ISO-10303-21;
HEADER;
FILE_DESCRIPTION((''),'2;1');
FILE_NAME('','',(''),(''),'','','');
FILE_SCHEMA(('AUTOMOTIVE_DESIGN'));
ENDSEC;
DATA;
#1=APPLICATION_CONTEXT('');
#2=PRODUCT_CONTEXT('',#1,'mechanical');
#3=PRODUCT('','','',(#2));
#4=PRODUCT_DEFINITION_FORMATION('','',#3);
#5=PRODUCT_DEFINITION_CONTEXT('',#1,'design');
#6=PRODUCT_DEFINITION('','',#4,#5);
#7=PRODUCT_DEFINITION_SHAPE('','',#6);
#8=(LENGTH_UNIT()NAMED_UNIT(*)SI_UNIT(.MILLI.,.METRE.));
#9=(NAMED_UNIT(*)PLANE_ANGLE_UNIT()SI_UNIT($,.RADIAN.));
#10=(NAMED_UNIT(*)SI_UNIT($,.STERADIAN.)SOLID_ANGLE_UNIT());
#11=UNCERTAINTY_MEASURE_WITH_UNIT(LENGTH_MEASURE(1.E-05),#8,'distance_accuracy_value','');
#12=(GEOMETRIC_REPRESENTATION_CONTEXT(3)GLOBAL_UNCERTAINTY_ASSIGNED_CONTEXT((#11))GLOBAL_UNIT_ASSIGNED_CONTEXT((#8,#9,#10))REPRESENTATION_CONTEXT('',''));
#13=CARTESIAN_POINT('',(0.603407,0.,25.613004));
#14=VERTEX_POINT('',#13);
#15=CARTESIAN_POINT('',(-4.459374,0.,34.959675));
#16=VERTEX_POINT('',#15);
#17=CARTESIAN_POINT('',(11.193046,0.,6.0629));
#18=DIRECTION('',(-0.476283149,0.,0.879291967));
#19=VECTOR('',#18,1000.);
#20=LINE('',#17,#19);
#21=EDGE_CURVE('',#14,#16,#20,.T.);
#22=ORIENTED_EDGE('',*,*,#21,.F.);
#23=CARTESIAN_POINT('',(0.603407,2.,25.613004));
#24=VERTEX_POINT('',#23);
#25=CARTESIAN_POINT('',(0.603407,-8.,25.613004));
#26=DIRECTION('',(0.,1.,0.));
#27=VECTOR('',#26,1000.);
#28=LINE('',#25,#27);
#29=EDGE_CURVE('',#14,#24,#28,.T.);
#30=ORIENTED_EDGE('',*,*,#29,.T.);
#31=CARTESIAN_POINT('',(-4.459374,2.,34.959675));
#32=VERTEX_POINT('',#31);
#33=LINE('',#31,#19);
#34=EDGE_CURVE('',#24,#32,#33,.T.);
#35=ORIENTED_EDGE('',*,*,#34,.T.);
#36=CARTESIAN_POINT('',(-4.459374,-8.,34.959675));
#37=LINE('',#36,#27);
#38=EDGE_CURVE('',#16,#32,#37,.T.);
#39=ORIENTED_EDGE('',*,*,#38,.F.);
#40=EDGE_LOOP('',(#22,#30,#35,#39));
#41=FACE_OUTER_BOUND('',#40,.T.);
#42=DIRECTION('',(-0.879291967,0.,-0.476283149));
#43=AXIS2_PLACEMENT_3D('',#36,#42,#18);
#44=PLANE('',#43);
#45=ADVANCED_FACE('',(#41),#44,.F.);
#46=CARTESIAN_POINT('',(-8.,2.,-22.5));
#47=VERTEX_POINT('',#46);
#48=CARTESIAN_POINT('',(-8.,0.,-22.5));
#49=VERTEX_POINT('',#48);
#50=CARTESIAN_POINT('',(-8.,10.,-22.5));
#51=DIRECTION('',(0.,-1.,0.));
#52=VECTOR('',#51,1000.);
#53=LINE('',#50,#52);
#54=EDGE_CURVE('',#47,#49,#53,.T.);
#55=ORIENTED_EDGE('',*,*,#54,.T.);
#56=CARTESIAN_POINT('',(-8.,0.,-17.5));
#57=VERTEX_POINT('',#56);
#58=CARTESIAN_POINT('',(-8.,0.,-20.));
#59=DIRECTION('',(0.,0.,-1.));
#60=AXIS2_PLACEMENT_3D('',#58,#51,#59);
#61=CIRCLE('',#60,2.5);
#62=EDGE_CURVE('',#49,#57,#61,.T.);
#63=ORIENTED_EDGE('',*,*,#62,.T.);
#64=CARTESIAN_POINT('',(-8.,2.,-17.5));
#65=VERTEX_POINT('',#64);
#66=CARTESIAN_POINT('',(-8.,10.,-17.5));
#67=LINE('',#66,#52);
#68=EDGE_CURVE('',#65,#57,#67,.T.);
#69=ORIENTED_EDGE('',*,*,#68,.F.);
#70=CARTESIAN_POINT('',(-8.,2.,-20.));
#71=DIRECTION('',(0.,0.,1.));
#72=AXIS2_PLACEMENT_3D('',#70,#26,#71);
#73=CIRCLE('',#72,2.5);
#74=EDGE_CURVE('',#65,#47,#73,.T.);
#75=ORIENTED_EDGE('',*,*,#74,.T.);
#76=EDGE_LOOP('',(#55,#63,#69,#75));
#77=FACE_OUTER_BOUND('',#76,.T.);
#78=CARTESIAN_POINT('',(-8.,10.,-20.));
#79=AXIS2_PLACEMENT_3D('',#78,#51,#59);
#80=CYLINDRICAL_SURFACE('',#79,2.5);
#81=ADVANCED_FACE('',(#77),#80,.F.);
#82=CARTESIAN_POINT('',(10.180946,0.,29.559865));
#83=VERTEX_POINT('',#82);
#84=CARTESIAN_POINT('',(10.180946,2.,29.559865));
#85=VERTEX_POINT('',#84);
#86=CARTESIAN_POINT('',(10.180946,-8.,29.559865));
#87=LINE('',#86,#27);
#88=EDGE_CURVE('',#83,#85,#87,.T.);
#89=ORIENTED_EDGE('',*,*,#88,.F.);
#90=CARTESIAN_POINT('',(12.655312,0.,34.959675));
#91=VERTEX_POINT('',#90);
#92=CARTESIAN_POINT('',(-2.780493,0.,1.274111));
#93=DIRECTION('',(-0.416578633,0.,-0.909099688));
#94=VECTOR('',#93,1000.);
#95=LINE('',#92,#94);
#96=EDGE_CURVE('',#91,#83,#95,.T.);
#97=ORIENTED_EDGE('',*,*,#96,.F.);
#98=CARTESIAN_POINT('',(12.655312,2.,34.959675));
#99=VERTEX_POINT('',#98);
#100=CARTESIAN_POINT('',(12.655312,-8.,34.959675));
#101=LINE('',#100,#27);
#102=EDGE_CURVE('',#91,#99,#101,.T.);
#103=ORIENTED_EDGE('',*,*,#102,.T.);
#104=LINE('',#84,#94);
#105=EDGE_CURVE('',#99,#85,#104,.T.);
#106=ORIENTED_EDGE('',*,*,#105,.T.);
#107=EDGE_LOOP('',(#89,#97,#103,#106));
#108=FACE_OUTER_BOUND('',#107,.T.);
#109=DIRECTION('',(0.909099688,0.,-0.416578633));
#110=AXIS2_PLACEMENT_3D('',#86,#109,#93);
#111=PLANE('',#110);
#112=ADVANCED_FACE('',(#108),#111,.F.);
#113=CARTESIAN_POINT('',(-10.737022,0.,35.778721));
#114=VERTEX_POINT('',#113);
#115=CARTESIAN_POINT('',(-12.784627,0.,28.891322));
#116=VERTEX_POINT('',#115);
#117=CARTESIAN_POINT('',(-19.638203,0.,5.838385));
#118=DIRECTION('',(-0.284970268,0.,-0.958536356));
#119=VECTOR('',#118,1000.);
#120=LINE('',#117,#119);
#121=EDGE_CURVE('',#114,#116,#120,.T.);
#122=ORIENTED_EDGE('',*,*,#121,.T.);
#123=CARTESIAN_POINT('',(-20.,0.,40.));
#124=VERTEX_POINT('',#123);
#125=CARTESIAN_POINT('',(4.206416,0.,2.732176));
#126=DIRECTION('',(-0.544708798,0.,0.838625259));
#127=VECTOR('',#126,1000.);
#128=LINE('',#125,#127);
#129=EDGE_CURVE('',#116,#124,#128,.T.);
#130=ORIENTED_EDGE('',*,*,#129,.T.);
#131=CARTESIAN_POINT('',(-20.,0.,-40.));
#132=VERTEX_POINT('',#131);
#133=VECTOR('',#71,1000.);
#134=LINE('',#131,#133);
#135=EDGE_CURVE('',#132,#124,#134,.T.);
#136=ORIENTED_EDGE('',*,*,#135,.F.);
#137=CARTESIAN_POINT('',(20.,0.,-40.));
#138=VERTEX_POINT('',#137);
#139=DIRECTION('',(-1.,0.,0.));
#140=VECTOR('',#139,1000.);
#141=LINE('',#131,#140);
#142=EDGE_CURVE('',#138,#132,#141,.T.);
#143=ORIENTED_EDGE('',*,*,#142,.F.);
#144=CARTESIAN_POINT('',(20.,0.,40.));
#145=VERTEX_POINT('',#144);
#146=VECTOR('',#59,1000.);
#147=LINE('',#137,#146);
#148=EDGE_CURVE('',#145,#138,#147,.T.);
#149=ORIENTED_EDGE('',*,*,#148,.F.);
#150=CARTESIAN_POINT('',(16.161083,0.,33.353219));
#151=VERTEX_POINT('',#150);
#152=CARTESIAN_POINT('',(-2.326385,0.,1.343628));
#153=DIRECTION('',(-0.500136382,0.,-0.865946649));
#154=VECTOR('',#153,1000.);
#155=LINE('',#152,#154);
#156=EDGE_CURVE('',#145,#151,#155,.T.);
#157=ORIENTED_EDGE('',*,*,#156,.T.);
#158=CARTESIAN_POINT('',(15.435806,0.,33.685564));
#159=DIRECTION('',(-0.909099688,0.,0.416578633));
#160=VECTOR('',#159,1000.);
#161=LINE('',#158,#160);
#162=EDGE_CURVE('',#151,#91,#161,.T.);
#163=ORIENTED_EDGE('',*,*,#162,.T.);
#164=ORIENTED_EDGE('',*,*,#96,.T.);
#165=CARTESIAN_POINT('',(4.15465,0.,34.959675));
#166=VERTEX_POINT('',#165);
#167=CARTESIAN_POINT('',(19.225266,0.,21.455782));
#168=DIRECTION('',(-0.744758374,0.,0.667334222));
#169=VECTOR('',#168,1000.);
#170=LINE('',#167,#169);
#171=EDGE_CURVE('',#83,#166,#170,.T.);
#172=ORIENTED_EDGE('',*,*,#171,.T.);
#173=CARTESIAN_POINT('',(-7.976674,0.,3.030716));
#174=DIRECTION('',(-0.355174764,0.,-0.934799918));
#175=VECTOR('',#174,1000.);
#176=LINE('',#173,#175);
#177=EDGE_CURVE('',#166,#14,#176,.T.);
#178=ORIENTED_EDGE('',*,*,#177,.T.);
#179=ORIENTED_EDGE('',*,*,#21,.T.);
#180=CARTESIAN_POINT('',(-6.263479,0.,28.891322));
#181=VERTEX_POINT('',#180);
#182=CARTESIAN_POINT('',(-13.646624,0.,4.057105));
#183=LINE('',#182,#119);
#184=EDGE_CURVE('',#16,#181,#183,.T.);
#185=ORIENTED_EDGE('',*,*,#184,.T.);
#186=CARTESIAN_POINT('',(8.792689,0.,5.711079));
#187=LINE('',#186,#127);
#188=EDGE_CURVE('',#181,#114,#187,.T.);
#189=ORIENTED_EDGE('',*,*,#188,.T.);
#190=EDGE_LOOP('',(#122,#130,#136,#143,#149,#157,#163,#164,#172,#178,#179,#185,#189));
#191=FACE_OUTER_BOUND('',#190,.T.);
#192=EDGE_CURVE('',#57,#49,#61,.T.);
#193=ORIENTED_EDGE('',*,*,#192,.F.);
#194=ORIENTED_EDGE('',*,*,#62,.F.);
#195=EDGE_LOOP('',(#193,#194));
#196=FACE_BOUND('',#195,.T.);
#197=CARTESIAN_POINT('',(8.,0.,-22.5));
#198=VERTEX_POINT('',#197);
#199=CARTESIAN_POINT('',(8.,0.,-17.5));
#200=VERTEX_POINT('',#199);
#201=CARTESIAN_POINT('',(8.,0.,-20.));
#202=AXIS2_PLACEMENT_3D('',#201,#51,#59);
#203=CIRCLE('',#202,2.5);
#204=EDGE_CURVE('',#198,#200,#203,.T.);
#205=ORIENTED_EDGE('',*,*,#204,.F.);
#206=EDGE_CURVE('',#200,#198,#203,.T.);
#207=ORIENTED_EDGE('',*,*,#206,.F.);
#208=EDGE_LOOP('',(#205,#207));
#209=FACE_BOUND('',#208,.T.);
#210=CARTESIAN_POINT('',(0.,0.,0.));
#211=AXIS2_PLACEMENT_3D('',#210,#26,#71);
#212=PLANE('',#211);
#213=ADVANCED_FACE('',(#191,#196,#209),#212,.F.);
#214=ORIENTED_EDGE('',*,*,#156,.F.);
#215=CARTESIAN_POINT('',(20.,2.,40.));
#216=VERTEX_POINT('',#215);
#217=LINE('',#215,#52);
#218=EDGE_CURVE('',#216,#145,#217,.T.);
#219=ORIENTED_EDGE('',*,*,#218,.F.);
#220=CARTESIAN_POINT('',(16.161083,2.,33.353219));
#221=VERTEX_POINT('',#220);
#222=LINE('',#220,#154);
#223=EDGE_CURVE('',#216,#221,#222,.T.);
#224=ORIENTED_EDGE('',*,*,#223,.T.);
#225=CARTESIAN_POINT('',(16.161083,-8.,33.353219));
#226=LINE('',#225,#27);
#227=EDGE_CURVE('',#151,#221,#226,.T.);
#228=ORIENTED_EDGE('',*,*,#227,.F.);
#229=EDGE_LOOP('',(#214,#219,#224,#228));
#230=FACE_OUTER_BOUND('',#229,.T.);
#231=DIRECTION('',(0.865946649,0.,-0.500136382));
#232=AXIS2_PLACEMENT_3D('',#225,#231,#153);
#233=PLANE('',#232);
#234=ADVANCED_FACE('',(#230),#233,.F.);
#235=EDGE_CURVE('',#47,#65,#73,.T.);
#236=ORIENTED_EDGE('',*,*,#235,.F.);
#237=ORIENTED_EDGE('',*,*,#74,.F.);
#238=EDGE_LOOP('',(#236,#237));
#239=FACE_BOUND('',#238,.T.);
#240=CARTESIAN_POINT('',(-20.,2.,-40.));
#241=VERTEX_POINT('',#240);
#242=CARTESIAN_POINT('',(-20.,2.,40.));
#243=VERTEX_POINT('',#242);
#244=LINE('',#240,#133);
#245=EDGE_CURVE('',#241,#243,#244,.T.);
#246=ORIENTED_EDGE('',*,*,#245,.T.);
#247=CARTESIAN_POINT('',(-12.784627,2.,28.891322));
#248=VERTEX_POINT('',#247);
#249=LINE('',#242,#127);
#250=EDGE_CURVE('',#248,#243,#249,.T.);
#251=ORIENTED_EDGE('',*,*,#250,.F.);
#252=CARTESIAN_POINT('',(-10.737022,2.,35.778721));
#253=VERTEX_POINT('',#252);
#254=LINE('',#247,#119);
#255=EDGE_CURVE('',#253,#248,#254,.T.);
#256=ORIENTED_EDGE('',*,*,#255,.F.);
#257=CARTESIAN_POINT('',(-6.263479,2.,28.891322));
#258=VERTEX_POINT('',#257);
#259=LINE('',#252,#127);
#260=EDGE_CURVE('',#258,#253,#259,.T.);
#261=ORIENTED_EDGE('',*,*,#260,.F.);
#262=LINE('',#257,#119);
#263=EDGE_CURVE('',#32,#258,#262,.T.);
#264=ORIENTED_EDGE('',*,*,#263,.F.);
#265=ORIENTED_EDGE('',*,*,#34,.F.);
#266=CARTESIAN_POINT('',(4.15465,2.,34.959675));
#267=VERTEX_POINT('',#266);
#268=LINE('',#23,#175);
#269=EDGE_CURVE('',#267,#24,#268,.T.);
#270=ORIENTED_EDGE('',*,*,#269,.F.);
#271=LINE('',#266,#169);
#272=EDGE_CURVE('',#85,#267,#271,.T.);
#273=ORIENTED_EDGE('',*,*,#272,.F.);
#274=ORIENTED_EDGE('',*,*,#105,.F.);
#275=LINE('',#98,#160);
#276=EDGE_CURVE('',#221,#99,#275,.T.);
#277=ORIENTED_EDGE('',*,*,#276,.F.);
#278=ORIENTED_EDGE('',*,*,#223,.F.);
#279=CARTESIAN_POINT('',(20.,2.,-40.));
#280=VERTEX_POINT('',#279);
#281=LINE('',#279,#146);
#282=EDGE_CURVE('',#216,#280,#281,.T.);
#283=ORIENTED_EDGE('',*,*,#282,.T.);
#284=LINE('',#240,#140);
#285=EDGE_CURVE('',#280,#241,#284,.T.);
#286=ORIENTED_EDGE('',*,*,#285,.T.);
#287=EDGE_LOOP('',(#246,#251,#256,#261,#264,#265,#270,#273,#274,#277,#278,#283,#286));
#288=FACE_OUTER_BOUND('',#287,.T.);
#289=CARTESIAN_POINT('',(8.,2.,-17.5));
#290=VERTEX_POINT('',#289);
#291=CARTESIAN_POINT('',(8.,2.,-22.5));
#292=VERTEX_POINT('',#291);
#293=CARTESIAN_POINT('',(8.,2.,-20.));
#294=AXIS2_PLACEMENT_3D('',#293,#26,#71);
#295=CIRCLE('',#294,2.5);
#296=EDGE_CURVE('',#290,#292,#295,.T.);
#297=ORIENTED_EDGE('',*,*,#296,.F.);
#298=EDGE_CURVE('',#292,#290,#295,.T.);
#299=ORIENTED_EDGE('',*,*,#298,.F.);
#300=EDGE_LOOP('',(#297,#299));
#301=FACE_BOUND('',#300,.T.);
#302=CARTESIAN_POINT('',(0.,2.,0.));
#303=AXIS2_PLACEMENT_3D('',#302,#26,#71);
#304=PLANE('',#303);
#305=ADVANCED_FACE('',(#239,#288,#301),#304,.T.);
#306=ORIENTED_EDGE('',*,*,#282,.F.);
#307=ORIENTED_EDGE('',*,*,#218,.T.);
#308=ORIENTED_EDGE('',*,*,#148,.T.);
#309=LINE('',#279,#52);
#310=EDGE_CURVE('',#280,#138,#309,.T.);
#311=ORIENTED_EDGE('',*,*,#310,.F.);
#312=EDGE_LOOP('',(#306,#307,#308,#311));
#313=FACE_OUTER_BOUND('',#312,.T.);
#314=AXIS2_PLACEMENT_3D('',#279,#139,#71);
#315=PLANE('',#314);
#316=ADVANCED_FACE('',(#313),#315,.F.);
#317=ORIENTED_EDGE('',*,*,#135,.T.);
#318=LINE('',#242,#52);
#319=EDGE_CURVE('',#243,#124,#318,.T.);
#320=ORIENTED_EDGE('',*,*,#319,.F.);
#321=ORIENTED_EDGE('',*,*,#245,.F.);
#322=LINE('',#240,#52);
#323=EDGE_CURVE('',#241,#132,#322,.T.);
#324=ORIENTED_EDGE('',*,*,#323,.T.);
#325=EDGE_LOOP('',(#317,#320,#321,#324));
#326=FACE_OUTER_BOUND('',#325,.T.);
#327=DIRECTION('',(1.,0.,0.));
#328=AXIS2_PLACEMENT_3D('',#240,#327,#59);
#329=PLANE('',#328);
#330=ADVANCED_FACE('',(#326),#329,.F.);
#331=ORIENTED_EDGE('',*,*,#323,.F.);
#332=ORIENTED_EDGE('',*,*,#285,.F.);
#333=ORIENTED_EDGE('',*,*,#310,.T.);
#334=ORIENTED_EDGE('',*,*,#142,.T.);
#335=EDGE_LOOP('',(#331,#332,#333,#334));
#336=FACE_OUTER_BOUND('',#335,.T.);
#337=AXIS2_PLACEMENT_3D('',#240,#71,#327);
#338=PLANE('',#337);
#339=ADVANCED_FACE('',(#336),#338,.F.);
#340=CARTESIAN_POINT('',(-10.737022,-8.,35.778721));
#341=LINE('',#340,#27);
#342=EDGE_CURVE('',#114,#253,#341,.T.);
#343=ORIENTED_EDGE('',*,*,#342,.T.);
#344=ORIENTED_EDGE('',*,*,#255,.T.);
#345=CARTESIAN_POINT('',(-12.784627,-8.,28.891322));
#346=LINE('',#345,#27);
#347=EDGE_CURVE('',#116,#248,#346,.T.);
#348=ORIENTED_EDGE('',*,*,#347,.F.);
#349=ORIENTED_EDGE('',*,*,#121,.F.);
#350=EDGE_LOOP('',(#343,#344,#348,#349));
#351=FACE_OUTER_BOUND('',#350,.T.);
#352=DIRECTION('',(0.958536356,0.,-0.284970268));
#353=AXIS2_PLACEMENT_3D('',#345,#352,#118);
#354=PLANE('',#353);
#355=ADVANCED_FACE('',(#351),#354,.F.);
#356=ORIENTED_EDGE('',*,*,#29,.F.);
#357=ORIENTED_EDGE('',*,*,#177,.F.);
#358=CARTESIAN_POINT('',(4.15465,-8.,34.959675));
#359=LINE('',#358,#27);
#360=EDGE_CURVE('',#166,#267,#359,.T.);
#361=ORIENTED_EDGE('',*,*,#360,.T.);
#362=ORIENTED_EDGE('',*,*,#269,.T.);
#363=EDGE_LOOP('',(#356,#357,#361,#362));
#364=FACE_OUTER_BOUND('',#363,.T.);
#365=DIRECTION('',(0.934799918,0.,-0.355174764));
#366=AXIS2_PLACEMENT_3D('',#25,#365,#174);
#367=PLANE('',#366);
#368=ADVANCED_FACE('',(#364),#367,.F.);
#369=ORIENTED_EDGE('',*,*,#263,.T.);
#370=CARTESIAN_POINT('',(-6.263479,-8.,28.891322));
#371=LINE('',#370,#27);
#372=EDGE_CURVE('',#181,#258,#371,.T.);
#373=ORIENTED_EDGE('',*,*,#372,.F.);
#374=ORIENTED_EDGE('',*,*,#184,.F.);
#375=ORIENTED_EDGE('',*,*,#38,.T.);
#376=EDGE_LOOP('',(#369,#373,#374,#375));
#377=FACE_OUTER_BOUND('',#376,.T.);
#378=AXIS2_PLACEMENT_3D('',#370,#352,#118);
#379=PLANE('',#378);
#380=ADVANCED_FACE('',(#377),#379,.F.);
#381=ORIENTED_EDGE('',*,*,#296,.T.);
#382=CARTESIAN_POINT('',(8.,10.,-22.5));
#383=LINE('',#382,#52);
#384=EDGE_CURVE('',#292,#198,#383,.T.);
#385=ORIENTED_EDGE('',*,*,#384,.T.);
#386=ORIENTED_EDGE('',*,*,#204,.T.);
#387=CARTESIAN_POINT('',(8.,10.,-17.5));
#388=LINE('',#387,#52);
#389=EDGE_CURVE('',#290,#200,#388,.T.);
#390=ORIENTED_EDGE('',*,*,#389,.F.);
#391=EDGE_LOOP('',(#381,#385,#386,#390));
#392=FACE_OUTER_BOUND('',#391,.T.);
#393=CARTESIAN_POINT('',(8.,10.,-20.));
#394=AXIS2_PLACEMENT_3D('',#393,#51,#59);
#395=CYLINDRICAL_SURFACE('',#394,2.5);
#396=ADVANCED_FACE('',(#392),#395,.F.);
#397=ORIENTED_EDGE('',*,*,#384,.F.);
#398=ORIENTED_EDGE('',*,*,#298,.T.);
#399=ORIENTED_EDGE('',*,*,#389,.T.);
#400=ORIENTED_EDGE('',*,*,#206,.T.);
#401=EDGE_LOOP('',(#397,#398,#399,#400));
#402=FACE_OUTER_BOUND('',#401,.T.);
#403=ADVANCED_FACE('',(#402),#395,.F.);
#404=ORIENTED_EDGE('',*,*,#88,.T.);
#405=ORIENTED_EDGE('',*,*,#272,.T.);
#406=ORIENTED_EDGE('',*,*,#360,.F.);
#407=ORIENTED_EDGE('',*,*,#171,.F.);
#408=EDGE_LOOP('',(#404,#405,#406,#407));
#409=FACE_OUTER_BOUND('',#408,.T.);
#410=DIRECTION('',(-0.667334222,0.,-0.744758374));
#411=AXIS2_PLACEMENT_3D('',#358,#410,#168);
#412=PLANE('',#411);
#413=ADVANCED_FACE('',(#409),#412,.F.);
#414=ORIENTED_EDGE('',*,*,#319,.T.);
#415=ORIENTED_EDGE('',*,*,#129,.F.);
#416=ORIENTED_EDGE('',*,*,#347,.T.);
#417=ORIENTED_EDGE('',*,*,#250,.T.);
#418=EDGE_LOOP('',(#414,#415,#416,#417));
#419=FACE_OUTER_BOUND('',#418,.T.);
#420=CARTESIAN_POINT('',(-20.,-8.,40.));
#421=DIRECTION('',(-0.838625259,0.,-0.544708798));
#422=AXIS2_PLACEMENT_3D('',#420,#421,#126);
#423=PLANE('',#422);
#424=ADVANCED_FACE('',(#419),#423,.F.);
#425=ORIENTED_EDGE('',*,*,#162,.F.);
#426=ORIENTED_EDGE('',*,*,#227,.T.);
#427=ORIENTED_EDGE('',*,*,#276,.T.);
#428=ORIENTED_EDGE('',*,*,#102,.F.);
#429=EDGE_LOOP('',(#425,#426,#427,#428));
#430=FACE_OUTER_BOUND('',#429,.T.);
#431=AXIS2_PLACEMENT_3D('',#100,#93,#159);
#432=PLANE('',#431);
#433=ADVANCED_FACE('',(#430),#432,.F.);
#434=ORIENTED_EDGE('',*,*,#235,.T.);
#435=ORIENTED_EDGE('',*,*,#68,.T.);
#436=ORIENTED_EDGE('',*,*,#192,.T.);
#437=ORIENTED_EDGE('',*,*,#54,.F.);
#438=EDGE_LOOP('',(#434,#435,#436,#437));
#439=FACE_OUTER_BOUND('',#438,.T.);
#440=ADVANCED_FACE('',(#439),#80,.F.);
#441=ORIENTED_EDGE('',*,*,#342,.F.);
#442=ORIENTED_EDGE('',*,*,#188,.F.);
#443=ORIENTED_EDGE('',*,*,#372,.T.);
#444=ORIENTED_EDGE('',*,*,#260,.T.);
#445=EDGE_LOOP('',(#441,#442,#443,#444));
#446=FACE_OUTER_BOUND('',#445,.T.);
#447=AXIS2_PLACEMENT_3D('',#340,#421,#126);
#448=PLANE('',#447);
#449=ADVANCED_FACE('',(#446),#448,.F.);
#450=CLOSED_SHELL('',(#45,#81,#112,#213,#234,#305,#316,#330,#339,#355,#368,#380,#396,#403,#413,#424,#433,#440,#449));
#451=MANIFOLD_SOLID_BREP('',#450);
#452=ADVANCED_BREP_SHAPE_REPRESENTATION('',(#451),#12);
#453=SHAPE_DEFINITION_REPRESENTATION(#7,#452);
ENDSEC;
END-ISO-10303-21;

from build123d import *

# Parameters (mm, degrees)
SKETCH1_W           = 40
SKETCH1_H           = 80
BOSS_EXTRUDE1_DEPTH = 2
SKETCH2_R           = 2.5
CUT_EXTRUDE1_DEPTH  = 10
CUT_EXTRUDE2_DEPTH  = 10


with BuildPart() as part:
    # Sketch1 → Boss-Extrude1 (new body)
    with BuildSketch(Plane(origin=(0, 0, 0), x_dir=(1, 0, 0), z_dir=(0, 1, 0))):
        Rectangle(SKETCH1_W, SKETCH1_H)
    extrude(amount=BOSS_EXTRUDE1_DEPTH)

    # Sketch2 → Cut-Extrude1 (cut)
    with BuildSketch(Plane.XZ):
        with Locations(Location((8, -20, 0), (0, 0, 270))):
            Circle(SKETCH2_R)
        with Locations(Location((-8, -20, 0), (0, 0, 270))):
            Circle(SKETCH2_R)
    extrude(amount=-CUT_EXTRUDE1_DEPTH, mode=Mode.SUBTRACT)

    # Sketch3 → Cut-Extrude2 (cut)
    with BuildSketch(Plane(origin=(0, 2, 0), x_dir=(1, 0, 0), z_dir=(0, 1, 0))):
        Polygon((-20, -40), (-12.784626592, -28.891322442), (-10.73702175, -35.778720546), (-6.263478534, -28.891322442), (-4.459373627, -34.959675311), (0.603406691, -25.613003955), (4.154649825, -34.959675311), (10.180946182, -29.559865215), (12.65531235, -34.959675311), (16.161083178, -33.353218681), (20, -40), align=None)
    extrude(amount=-CUT_EXTRUDE2_DEPTH, mode=Mode.SUBTRACT)


solid = part.part
